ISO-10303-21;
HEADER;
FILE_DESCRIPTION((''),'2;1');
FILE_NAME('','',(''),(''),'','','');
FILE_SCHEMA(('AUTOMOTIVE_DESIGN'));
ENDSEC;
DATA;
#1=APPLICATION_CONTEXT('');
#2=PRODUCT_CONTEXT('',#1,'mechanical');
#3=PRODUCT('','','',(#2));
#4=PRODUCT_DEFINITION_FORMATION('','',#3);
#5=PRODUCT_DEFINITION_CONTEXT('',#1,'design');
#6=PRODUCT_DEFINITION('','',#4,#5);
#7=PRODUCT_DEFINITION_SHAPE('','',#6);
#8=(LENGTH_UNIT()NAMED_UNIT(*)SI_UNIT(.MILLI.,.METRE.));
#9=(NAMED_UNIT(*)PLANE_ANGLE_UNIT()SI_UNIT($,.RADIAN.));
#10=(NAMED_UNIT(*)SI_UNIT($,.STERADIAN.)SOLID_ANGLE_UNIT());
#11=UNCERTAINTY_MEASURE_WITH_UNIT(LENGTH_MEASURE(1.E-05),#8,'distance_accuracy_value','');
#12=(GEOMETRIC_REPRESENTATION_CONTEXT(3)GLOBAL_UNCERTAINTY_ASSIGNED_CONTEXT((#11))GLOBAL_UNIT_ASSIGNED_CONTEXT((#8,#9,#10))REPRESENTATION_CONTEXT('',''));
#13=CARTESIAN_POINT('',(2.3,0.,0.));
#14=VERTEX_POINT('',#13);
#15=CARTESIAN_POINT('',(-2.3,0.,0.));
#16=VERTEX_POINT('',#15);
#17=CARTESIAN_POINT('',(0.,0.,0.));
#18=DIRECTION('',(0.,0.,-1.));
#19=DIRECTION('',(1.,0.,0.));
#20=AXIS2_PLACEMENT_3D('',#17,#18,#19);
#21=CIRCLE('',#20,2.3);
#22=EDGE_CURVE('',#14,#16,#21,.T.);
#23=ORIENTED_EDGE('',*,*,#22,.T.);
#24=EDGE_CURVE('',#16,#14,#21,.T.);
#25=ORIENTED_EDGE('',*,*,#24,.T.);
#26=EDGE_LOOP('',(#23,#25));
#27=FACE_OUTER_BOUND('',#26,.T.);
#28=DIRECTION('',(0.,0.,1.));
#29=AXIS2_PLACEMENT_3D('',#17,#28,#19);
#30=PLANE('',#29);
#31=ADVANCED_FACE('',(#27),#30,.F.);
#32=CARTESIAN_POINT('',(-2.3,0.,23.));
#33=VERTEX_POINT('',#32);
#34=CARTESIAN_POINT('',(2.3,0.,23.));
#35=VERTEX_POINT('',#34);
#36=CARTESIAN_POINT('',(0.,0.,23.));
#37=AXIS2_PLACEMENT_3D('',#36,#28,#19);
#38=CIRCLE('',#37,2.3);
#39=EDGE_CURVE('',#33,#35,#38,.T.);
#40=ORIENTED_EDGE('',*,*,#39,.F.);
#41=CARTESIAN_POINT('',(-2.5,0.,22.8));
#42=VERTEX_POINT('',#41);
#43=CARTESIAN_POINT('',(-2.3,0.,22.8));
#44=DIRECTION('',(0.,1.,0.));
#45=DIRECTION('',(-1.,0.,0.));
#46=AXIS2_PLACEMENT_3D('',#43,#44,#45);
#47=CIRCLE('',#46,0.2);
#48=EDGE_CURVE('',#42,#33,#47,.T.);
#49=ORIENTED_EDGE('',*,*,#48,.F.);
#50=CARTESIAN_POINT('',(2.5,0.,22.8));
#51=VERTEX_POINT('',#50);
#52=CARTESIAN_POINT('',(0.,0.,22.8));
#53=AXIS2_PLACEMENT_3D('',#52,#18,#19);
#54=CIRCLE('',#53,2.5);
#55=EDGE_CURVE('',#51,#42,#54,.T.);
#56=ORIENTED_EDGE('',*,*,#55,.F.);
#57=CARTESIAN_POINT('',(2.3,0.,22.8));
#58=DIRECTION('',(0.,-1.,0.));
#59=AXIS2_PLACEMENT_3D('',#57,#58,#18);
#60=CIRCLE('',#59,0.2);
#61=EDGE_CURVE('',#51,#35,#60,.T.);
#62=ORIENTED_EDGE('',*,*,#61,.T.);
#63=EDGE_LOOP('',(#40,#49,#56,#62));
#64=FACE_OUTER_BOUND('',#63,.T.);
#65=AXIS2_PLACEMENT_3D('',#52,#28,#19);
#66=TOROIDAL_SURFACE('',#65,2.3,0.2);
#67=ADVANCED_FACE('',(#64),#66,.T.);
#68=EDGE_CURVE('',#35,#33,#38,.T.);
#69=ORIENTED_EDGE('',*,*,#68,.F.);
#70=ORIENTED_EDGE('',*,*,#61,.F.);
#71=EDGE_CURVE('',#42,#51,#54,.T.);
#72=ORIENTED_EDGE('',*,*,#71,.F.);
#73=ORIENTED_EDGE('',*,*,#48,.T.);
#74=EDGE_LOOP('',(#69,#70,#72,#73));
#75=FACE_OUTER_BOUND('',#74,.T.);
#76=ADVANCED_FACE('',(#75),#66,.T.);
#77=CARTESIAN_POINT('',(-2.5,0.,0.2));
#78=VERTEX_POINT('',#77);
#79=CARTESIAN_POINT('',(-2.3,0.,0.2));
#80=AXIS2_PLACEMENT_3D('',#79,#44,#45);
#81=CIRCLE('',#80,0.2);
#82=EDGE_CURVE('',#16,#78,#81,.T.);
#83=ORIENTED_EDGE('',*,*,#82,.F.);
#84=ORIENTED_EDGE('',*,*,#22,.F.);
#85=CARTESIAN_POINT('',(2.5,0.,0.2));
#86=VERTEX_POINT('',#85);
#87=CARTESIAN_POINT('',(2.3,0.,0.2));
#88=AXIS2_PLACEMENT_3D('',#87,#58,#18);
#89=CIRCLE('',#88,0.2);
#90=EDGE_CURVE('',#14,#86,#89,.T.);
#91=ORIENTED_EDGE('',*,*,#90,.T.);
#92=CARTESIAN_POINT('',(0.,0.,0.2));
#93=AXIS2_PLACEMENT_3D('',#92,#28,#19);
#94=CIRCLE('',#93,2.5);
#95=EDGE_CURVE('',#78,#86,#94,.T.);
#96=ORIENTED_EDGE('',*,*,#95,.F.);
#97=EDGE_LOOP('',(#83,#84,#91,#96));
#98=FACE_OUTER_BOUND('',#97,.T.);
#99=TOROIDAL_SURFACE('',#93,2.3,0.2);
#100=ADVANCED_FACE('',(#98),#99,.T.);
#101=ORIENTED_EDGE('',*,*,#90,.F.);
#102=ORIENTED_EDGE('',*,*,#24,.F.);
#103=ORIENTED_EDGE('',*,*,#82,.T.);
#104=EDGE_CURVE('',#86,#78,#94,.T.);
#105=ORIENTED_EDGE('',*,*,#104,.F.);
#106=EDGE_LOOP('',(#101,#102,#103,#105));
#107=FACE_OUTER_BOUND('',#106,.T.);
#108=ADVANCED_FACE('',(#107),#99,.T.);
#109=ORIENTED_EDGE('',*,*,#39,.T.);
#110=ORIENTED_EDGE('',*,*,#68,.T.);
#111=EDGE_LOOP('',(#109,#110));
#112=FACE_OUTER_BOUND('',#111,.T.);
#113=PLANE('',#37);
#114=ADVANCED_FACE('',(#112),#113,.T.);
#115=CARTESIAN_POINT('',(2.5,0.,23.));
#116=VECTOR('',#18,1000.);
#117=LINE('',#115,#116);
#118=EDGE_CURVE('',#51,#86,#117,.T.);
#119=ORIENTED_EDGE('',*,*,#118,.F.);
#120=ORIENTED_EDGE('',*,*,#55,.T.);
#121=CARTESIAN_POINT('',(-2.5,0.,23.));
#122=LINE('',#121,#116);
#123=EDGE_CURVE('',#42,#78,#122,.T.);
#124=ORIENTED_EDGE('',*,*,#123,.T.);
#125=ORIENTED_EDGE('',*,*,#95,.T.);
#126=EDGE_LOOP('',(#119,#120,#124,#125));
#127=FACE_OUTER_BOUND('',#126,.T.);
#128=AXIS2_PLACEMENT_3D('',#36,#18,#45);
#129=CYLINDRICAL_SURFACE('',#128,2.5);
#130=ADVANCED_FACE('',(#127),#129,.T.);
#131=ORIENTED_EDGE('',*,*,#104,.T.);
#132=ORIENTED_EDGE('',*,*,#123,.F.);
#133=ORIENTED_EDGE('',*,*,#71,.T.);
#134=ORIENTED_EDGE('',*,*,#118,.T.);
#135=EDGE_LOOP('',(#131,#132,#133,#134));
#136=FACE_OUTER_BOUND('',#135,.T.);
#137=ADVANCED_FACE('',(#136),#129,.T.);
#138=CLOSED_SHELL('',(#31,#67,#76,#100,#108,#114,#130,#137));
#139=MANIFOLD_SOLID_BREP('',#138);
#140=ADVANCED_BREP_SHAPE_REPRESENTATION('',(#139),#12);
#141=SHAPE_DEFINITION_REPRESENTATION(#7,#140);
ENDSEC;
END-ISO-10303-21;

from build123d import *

# Parameters (mm, degrees)
SKETCH_1_R      = 2.5
EXTRUDE_1_DEPTH = 23
FILLET_1_R      = 0.2


with BuildPart() as part:
    # 草图1 → 凸台-拉伸1 (new body)
    with BuildSketch(Plane.XY):
        Circle(SKETCH_1_R)
    extrude(amount=EXTRUDE_1_DEPTH)

    # 圆角1
    fillet_1_edges = [part.edges().sort_by_distance(p)[0] for p in [
        (-2.5, 0, 0),
        (-2.5, 0, 23),
    ]]
    fillet(fillet_1_edges, radius=FILLET_1_R)


solid = part.part
